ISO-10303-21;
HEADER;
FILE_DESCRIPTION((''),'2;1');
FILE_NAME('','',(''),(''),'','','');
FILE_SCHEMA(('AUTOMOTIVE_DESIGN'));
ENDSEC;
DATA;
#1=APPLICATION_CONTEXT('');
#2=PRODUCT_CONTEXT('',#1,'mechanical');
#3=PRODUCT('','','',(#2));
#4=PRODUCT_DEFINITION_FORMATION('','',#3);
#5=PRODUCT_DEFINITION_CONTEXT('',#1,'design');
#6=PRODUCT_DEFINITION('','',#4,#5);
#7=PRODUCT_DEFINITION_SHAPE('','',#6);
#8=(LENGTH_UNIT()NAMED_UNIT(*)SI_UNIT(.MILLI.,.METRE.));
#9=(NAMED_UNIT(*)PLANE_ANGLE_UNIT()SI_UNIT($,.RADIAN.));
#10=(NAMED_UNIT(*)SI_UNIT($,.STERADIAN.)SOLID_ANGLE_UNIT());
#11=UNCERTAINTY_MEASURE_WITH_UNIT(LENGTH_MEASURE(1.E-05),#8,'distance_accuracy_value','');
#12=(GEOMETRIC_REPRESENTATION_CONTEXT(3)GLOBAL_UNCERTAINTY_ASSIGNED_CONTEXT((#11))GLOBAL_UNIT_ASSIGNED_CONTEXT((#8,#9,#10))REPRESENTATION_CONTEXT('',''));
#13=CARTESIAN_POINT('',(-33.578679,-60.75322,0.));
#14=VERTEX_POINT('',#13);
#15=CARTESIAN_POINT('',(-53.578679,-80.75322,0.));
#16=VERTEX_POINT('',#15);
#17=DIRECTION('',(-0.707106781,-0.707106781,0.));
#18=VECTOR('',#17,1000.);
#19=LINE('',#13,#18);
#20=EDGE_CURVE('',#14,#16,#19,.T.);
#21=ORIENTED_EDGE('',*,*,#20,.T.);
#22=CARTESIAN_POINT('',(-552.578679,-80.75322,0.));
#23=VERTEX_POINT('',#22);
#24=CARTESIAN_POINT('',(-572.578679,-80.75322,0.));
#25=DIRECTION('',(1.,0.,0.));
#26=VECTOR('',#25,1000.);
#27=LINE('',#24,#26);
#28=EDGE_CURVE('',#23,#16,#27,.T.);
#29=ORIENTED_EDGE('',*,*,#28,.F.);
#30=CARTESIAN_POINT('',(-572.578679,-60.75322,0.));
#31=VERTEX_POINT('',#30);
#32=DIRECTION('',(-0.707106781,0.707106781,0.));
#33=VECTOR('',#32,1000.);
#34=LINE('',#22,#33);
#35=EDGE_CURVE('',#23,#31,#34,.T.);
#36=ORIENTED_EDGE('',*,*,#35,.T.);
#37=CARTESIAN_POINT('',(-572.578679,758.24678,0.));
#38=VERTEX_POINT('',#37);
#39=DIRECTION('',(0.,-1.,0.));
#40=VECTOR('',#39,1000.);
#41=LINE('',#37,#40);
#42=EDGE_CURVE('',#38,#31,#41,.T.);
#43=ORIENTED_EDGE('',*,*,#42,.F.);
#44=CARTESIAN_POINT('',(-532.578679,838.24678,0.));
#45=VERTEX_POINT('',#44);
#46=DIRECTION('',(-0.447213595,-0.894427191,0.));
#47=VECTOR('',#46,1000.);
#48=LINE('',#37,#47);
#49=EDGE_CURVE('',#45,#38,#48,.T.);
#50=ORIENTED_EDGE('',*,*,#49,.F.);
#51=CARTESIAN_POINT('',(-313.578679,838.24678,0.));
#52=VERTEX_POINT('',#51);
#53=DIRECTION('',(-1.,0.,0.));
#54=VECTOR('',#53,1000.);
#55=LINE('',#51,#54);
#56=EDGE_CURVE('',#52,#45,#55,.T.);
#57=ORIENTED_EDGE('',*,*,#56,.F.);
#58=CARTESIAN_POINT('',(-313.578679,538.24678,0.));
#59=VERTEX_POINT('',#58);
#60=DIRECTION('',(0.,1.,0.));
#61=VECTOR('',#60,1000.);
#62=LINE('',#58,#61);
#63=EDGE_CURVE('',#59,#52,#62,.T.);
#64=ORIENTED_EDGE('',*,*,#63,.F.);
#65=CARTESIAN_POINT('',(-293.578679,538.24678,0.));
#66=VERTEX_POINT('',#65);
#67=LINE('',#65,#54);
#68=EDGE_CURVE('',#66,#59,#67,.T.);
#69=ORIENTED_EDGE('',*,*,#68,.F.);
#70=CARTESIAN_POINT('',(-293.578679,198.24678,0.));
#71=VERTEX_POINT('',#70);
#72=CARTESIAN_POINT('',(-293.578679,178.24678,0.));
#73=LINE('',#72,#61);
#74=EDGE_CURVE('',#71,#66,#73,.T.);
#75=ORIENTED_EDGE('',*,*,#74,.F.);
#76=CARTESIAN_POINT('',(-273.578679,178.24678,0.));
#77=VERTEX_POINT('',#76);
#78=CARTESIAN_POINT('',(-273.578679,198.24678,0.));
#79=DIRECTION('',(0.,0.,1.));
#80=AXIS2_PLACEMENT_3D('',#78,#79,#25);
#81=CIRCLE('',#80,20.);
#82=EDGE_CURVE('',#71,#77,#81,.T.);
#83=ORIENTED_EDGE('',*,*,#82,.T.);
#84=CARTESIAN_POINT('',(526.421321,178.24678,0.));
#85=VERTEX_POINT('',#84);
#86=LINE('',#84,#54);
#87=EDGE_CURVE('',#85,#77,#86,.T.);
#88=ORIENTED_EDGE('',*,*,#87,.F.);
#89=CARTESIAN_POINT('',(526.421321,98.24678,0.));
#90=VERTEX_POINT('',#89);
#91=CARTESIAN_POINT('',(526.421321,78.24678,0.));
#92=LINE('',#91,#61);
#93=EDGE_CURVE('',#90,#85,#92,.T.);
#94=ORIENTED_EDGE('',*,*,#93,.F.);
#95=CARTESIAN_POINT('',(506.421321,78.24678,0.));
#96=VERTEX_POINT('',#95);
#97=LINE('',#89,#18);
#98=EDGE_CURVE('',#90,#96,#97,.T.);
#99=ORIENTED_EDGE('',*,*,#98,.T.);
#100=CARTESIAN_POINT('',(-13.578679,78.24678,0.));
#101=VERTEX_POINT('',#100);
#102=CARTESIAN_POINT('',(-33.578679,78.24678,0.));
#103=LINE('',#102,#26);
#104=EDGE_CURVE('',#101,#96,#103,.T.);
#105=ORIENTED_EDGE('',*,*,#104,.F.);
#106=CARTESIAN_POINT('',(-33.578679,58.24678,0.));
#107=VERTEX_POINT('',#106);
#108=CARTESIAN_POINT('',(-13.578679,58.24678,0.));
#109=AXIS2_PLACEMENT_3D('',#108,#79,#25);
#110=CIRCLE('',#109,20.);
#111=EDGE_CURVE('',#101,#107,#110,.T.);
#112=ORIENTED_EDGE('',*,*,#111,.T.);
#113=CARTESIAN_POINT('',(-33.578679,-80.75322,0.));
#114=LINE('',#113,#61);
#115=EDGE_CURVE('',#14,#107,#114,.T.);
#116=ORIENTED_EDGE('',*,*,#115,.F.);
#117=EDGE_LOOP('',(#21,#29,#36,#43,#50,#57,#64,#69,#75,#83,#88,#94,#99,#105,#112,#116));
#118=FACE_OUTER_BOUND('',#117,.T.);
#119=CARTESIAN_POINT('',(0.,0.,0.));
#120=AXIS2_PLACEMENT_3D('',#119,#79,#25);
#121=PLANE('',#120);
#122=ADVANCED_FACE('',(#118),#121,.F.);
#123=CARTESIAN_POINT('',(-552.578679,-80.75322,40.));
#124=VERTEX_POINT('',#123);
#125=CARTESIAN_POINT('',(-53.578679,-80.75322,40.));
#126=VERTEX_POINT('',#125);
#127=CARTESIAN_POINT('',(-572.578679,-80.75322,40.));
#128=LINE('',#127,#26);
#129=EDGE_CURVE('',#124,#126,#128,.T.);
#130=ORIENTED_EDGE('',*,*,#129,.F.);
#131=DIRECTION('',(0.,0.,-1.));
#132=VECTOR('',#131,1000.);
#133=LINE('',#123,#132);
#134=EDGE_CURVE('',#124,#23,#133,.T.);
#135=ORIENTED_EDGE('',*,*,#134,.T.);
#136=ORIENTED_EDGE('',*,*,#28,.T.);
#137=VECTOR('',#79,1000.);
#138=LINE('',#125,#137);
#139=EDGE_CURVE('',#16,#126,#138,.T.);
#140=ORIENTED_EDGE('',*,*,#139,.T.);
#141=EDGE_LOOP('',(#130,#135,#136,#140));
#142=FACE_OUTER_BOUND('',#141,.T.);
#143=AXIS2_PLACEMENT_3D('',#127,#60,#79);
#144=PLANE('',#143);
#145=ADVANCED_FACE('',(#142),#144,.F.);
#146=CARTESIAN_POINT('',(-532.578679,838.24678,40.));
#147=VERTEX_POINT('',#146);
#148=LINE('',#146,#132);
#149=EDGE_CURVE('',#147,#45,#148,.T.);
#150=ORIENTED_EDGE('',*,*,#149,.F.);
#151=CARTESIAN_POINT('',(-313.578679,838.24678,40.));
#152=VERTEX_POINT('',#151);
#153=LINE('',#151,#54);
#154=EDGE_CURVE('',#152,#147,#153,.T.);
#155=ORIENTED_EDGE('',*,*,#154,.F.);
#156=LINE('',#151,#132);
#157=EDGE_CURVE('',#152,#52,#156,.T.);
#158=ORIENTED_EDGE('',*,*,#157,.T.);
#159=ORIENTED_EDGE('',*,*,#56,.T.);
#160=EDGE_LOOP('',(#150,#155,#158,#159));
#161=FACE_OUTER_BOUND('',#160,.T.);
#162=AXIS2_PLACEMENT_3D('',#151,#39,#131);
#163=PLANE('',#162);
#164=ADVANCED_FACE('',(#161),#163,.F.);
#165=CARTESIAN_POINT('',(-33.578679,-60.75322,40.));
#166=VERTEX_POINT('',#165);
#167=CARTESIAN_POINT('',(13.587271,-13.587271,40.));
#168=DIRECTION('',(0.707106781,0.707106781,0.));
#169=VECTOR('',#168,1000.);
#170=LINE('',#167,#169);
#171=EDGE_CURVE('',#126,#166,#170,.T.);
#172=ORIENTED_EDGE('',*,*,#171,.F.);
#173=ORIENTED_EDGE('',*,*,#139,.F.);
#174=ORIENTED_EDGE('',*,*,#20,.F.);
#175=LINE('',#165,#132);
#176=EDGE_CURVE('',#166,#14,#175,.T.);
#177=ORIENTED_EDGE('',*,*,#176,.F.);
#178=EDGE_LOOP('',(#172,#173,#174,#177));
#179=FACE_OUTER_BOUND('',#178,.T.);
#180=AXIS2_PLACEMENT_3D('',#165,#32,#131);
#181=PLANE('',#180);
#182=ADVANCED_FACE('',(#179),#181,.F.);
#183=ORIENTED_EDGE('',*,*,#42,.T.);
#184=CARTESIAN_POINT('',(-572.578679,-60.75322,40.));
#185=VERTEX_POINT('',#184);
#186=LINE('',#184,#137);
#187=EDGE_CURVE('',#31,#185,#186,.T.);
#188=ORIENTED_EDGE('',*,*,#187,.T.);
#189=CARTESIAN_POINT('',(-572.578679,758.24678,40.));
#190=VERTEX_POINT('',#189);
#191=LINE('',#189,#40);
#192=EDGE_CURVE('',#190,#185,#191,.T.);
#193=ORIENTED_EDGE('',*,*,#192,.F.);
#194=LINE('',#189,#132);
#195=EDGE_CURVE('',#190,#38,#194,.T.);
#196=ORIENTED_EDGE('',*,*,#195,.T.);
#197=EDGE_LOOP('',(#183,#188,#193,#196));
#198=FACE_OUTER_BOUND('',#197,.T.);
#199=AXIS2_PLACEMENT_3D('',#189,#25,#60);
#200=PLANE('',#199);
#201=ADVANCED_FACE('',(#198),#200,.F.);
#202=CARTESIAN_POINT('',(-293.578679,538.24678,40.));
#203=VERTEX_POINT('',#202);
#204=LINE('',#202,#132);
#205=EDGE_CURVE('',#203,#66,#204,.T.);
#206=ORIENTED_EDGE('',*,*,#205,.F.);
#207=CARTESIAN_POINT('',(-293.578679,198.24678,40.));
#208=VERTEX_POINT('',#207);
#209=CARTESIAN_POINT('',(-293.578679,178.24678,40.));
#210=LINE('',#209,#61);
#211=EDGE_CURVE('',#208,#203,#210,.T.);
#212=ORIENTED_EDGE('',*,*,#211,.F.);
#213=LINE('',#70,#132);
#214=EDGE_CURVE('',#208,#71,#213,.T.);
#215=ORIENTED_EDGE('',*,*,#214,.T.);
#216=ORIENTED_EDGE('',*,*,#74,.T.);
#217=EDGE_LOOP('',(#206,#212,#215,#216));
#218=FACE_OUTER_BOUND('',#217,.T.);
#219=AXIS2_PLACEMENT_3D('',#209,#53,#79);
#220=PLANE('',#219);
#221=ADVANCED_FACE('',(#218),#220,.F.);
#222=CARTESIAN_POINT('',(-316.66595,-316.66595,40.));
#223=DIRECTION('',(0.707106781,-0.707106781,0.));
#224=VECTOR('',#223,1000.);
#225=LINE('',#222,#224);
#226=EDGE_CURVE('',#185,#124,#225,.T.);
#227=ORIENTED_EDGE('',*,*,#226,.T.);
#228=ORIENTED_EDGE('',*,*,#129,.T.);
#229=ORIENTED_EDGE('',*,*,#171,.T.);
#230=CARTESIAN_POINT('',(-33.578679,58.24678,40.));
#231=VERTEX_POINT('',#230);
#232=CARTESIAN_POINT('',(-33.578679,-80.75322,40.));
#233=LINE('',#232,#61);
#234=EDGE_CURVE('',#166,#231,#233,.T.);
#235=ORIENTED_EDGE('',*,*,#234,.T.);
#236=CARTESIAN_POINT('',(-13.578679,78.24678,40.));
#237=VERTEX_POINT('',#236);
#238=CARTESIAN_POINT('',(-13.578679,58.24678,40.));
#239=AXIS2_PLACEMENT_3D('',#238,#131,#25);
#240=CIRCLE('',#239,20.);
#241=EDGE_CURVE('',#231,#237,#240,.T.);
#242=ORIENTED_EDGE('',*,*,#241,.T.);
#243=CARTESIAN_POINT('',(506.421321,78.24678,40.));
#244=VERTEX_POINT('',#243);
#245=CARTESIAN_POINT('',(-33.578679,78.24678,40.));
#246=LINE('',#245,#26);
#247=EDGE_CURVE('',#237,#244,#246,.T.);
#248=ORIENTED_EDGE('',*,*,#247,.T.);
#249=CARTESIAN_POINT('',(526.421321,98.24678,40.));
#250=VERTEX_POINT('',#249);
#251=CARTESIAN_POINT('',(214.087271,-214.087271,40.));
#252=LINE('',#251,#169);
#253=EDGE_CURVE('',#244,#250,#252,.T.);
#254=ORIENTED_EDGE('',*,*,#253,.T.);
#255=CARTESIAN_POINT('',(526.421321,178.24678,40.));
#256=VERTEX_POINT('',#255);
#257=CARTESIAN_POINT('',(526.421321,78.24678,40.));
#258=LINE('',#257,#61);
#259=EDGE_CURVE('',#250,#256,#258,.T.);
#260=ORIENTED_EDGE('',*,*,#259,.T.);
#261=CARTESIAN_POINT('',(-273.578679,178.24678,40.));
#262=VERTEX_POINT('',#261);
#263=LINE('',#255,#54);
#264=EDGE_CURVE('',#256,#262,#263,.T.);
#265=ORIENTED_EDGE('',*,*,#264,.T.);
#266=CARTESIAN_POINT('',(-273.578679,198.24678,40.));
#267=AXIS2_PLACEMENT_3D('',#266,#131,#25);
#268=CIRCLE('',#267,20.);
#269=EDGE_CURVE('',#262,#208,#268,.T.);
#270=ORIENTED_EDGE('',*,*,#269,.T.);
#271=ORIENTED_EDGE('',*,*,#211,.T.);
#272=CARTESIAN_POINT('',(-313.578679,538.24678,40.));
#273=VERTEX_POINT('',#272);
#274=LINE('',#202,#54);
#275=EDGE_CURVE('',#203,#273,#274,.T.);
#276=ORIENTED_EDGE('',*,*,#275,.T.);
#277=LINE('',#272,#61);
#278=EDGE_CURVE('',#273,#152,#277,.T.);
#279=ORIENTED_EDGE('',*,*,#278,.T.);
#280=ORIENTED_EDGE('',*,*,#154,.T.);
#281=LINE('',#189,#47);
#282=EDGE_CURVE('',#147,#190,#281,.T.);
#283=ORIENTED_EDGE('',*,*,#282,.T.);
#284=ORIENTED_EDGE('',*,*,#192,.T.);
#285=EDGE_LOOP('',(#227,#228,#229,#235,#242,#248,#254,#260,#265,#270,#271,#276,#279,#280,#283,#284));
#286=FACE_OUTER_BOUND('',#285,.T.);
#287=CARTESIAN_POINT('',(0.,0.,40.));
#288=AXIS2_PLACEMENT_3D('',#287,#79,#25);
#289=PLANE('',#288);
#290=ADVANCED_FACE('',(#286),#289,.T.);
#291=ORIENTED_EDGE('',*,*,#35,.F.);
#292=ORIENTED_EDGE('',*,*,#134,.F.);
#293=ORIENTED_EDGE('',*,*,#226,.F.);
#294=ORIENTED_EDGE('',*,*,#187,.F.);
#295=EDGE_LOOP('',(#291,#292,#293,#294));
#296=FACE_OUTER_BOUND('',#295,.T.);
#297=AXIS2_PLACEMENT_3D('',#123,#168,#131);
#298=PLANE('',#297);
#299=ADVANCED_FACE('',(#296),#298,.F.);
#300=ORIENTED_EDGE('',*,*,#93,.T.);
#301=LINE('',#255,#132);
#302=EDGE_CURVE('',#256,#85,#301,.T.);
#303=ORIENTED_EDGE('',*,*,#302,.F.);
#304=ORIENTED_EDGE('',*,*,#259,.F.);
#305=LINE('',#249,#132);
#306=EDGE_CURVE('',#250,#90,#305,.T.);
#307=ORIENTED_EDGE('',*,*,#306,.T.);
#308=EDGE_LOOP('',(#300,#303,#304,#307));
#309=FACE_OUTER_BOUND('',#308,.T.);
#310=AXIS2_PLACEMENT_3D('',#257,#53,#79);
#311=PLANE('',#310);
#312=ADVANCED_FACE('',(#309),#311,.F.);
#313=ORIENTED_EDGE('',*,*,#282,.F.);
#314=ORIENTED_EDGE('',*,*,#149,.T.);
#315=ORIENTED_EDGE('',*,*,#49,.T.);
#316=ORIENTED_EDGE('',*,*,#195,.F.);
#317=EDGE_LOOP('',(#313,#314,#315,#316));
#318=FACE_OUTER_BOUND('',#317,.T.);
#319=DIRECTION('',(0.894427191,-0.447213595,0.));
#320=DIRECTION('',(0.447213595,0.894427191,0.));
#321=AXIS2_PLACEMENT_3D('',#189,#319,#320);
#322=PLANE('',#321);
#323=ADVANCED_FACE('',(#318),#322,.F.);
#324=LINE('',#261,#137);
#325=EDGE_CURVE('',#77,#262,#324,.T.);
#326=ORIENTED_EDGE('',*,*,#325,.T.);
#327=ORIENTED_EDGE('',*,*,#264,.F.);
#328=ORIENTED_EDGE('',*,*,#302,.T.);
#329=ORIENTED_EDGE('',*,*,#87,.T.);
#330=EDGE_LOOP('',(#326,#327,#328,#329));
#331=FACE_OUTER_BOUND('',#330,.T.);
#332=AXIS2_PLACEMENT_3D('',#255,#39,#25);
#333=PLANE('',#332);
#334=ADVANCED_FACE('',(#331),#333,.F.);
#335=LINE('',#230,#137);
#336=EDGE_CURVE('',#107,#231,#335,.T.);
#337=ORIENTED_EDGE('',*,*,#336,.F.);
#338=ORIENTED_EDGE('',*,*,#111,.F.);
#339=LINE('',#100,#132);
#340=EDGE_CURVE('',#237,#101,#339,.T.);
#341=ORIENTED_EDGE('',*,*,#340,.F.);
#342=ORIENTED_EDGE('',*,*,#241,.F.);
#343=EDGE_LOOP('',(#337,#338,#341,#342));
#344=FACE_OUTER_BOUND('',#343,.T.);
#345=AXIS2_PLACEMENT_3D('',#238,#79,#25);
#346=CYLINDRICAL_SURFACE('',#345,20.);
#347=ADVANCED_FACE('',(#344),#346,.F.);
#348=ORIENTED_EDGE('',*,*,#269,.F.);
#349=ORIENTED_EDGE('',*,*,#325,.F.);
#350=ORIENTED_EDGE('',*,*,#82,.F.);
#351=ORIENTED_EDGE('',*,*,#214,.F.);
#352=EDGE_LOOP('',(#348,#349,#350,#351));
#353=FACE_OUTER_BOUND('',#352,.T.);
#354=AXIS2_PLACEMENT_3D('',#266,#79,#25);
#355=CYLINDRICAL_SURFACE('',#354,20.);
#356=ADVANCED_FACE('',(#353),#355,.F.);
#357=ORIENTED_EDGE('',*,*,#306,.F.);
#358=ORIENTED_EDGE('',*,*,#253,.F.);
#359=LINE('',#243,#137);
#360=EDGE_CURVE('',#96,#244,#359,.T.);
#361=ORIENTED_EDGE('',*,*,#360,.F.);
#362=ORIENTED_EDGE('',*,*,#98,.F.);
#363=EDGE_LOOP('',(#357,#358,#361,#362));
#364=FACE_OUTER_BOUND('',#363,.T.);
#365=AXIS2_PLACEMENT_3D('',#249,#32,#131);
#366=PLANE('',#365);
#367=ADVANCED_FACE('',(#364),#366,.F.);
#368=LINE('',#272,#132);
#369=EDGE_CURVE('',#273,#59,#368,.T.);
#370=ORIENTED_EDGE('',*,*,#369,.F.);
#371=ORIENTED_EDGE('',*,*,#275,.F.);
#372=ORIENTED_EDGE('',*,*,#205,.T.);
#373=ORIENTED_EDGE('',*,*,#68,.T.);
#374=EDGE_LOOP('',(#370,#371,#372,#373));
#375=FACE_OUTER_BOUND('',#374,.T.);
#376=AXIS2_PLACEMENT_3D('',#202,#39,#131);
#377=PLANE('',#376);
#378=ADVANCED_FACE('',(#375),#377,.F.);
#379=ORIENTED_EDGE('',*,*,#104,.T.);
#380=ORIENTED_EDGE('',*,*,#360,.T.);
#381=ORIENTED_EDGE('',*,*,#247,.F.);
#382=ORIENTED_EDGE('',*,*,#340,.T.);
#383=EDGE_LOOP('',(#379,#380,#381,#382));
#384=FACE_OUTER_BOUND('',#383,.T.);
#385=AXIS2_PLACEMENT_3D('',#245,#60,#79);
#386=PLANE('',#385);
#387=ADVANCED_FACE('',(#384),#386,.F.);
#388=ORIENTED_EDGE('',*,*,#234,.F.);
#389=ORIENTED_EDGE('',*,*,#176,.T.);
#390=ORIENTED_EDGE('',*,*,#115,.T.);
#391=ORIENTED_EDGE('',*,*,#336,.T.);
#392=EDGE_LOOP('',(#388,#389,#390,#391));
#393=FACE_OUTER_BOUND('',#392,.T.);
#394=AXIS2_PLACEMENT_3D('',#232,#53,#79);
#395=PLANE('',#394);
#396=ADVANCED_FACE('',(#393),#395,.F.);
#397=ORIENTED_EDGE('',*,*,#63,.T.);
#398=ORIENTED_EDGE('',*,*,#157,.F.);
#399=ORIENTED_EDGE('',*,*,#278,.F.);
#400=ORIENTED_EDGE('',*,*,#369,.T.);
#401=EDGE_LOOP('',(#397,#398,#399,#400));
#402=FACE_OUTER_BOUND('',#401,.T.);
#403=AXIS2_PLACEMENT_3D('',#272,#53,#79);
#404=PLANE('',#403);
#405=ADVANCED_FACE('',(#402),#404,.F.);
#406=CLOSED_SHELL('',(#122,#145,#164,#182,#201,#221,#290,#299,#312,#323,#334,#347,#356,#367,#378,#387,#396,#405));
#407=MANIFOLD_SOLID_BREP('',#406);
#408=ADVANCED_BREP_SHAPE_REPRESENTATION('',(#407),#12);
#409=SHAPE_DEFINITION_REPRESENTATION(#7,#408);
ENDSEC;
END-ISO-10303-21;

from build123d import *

# Parameters (mm, degrees)
BOSS_EXTRUDE1_DEPTH = 40
CHAMFER1_SIZE       = 20
FILLET1_R           = 20


with BuildPart() as part:
    # Sketch1 → Boss-Extrude1 (new body)
    with BuildSketch(Plane.XY):
        Polygon((-572.578678855, 758.246779508), (-572.578678855, -80.753220492), (-33.578678855, -80.753220492), (-33.578678855, 78.246779508), (526.421321145, 78.246779508), (526.421321145, 178.246779508), (-293.578678855, 178.246779508), (-293.578678855, 538.246779508), (-313.578678855, 538.246779508), (-313.578678855, 838.246779508), (-532.578678855, 838.246779508), align=None)
    extrude(amount=BOSS_EXTRUDE1_DEPTH)

    # Chamfer1
    chamfer1_edges = [part.edges().sort_by_distance(p)[0] for p in [
        (-572.578678855, -80.753220492, 20),
        (526.421321145, 78.246779508, 20),
        (-33.578678855, -80.753220492, 20),
    ]]
    chamfer(chamfer1_edges, length=CHAMFER1_SIZE)

    # Fillet1
    fillet1_edges = [part.edges().sort_by_distance(p)[0] for p in [
        (-293.578678855, 178.246779508, 20),
        (-33.578678855, 78.246779508, 20),
    ]]
    fillet(fillet1_edges, radius=FILLET1_R)


solid = part.part
